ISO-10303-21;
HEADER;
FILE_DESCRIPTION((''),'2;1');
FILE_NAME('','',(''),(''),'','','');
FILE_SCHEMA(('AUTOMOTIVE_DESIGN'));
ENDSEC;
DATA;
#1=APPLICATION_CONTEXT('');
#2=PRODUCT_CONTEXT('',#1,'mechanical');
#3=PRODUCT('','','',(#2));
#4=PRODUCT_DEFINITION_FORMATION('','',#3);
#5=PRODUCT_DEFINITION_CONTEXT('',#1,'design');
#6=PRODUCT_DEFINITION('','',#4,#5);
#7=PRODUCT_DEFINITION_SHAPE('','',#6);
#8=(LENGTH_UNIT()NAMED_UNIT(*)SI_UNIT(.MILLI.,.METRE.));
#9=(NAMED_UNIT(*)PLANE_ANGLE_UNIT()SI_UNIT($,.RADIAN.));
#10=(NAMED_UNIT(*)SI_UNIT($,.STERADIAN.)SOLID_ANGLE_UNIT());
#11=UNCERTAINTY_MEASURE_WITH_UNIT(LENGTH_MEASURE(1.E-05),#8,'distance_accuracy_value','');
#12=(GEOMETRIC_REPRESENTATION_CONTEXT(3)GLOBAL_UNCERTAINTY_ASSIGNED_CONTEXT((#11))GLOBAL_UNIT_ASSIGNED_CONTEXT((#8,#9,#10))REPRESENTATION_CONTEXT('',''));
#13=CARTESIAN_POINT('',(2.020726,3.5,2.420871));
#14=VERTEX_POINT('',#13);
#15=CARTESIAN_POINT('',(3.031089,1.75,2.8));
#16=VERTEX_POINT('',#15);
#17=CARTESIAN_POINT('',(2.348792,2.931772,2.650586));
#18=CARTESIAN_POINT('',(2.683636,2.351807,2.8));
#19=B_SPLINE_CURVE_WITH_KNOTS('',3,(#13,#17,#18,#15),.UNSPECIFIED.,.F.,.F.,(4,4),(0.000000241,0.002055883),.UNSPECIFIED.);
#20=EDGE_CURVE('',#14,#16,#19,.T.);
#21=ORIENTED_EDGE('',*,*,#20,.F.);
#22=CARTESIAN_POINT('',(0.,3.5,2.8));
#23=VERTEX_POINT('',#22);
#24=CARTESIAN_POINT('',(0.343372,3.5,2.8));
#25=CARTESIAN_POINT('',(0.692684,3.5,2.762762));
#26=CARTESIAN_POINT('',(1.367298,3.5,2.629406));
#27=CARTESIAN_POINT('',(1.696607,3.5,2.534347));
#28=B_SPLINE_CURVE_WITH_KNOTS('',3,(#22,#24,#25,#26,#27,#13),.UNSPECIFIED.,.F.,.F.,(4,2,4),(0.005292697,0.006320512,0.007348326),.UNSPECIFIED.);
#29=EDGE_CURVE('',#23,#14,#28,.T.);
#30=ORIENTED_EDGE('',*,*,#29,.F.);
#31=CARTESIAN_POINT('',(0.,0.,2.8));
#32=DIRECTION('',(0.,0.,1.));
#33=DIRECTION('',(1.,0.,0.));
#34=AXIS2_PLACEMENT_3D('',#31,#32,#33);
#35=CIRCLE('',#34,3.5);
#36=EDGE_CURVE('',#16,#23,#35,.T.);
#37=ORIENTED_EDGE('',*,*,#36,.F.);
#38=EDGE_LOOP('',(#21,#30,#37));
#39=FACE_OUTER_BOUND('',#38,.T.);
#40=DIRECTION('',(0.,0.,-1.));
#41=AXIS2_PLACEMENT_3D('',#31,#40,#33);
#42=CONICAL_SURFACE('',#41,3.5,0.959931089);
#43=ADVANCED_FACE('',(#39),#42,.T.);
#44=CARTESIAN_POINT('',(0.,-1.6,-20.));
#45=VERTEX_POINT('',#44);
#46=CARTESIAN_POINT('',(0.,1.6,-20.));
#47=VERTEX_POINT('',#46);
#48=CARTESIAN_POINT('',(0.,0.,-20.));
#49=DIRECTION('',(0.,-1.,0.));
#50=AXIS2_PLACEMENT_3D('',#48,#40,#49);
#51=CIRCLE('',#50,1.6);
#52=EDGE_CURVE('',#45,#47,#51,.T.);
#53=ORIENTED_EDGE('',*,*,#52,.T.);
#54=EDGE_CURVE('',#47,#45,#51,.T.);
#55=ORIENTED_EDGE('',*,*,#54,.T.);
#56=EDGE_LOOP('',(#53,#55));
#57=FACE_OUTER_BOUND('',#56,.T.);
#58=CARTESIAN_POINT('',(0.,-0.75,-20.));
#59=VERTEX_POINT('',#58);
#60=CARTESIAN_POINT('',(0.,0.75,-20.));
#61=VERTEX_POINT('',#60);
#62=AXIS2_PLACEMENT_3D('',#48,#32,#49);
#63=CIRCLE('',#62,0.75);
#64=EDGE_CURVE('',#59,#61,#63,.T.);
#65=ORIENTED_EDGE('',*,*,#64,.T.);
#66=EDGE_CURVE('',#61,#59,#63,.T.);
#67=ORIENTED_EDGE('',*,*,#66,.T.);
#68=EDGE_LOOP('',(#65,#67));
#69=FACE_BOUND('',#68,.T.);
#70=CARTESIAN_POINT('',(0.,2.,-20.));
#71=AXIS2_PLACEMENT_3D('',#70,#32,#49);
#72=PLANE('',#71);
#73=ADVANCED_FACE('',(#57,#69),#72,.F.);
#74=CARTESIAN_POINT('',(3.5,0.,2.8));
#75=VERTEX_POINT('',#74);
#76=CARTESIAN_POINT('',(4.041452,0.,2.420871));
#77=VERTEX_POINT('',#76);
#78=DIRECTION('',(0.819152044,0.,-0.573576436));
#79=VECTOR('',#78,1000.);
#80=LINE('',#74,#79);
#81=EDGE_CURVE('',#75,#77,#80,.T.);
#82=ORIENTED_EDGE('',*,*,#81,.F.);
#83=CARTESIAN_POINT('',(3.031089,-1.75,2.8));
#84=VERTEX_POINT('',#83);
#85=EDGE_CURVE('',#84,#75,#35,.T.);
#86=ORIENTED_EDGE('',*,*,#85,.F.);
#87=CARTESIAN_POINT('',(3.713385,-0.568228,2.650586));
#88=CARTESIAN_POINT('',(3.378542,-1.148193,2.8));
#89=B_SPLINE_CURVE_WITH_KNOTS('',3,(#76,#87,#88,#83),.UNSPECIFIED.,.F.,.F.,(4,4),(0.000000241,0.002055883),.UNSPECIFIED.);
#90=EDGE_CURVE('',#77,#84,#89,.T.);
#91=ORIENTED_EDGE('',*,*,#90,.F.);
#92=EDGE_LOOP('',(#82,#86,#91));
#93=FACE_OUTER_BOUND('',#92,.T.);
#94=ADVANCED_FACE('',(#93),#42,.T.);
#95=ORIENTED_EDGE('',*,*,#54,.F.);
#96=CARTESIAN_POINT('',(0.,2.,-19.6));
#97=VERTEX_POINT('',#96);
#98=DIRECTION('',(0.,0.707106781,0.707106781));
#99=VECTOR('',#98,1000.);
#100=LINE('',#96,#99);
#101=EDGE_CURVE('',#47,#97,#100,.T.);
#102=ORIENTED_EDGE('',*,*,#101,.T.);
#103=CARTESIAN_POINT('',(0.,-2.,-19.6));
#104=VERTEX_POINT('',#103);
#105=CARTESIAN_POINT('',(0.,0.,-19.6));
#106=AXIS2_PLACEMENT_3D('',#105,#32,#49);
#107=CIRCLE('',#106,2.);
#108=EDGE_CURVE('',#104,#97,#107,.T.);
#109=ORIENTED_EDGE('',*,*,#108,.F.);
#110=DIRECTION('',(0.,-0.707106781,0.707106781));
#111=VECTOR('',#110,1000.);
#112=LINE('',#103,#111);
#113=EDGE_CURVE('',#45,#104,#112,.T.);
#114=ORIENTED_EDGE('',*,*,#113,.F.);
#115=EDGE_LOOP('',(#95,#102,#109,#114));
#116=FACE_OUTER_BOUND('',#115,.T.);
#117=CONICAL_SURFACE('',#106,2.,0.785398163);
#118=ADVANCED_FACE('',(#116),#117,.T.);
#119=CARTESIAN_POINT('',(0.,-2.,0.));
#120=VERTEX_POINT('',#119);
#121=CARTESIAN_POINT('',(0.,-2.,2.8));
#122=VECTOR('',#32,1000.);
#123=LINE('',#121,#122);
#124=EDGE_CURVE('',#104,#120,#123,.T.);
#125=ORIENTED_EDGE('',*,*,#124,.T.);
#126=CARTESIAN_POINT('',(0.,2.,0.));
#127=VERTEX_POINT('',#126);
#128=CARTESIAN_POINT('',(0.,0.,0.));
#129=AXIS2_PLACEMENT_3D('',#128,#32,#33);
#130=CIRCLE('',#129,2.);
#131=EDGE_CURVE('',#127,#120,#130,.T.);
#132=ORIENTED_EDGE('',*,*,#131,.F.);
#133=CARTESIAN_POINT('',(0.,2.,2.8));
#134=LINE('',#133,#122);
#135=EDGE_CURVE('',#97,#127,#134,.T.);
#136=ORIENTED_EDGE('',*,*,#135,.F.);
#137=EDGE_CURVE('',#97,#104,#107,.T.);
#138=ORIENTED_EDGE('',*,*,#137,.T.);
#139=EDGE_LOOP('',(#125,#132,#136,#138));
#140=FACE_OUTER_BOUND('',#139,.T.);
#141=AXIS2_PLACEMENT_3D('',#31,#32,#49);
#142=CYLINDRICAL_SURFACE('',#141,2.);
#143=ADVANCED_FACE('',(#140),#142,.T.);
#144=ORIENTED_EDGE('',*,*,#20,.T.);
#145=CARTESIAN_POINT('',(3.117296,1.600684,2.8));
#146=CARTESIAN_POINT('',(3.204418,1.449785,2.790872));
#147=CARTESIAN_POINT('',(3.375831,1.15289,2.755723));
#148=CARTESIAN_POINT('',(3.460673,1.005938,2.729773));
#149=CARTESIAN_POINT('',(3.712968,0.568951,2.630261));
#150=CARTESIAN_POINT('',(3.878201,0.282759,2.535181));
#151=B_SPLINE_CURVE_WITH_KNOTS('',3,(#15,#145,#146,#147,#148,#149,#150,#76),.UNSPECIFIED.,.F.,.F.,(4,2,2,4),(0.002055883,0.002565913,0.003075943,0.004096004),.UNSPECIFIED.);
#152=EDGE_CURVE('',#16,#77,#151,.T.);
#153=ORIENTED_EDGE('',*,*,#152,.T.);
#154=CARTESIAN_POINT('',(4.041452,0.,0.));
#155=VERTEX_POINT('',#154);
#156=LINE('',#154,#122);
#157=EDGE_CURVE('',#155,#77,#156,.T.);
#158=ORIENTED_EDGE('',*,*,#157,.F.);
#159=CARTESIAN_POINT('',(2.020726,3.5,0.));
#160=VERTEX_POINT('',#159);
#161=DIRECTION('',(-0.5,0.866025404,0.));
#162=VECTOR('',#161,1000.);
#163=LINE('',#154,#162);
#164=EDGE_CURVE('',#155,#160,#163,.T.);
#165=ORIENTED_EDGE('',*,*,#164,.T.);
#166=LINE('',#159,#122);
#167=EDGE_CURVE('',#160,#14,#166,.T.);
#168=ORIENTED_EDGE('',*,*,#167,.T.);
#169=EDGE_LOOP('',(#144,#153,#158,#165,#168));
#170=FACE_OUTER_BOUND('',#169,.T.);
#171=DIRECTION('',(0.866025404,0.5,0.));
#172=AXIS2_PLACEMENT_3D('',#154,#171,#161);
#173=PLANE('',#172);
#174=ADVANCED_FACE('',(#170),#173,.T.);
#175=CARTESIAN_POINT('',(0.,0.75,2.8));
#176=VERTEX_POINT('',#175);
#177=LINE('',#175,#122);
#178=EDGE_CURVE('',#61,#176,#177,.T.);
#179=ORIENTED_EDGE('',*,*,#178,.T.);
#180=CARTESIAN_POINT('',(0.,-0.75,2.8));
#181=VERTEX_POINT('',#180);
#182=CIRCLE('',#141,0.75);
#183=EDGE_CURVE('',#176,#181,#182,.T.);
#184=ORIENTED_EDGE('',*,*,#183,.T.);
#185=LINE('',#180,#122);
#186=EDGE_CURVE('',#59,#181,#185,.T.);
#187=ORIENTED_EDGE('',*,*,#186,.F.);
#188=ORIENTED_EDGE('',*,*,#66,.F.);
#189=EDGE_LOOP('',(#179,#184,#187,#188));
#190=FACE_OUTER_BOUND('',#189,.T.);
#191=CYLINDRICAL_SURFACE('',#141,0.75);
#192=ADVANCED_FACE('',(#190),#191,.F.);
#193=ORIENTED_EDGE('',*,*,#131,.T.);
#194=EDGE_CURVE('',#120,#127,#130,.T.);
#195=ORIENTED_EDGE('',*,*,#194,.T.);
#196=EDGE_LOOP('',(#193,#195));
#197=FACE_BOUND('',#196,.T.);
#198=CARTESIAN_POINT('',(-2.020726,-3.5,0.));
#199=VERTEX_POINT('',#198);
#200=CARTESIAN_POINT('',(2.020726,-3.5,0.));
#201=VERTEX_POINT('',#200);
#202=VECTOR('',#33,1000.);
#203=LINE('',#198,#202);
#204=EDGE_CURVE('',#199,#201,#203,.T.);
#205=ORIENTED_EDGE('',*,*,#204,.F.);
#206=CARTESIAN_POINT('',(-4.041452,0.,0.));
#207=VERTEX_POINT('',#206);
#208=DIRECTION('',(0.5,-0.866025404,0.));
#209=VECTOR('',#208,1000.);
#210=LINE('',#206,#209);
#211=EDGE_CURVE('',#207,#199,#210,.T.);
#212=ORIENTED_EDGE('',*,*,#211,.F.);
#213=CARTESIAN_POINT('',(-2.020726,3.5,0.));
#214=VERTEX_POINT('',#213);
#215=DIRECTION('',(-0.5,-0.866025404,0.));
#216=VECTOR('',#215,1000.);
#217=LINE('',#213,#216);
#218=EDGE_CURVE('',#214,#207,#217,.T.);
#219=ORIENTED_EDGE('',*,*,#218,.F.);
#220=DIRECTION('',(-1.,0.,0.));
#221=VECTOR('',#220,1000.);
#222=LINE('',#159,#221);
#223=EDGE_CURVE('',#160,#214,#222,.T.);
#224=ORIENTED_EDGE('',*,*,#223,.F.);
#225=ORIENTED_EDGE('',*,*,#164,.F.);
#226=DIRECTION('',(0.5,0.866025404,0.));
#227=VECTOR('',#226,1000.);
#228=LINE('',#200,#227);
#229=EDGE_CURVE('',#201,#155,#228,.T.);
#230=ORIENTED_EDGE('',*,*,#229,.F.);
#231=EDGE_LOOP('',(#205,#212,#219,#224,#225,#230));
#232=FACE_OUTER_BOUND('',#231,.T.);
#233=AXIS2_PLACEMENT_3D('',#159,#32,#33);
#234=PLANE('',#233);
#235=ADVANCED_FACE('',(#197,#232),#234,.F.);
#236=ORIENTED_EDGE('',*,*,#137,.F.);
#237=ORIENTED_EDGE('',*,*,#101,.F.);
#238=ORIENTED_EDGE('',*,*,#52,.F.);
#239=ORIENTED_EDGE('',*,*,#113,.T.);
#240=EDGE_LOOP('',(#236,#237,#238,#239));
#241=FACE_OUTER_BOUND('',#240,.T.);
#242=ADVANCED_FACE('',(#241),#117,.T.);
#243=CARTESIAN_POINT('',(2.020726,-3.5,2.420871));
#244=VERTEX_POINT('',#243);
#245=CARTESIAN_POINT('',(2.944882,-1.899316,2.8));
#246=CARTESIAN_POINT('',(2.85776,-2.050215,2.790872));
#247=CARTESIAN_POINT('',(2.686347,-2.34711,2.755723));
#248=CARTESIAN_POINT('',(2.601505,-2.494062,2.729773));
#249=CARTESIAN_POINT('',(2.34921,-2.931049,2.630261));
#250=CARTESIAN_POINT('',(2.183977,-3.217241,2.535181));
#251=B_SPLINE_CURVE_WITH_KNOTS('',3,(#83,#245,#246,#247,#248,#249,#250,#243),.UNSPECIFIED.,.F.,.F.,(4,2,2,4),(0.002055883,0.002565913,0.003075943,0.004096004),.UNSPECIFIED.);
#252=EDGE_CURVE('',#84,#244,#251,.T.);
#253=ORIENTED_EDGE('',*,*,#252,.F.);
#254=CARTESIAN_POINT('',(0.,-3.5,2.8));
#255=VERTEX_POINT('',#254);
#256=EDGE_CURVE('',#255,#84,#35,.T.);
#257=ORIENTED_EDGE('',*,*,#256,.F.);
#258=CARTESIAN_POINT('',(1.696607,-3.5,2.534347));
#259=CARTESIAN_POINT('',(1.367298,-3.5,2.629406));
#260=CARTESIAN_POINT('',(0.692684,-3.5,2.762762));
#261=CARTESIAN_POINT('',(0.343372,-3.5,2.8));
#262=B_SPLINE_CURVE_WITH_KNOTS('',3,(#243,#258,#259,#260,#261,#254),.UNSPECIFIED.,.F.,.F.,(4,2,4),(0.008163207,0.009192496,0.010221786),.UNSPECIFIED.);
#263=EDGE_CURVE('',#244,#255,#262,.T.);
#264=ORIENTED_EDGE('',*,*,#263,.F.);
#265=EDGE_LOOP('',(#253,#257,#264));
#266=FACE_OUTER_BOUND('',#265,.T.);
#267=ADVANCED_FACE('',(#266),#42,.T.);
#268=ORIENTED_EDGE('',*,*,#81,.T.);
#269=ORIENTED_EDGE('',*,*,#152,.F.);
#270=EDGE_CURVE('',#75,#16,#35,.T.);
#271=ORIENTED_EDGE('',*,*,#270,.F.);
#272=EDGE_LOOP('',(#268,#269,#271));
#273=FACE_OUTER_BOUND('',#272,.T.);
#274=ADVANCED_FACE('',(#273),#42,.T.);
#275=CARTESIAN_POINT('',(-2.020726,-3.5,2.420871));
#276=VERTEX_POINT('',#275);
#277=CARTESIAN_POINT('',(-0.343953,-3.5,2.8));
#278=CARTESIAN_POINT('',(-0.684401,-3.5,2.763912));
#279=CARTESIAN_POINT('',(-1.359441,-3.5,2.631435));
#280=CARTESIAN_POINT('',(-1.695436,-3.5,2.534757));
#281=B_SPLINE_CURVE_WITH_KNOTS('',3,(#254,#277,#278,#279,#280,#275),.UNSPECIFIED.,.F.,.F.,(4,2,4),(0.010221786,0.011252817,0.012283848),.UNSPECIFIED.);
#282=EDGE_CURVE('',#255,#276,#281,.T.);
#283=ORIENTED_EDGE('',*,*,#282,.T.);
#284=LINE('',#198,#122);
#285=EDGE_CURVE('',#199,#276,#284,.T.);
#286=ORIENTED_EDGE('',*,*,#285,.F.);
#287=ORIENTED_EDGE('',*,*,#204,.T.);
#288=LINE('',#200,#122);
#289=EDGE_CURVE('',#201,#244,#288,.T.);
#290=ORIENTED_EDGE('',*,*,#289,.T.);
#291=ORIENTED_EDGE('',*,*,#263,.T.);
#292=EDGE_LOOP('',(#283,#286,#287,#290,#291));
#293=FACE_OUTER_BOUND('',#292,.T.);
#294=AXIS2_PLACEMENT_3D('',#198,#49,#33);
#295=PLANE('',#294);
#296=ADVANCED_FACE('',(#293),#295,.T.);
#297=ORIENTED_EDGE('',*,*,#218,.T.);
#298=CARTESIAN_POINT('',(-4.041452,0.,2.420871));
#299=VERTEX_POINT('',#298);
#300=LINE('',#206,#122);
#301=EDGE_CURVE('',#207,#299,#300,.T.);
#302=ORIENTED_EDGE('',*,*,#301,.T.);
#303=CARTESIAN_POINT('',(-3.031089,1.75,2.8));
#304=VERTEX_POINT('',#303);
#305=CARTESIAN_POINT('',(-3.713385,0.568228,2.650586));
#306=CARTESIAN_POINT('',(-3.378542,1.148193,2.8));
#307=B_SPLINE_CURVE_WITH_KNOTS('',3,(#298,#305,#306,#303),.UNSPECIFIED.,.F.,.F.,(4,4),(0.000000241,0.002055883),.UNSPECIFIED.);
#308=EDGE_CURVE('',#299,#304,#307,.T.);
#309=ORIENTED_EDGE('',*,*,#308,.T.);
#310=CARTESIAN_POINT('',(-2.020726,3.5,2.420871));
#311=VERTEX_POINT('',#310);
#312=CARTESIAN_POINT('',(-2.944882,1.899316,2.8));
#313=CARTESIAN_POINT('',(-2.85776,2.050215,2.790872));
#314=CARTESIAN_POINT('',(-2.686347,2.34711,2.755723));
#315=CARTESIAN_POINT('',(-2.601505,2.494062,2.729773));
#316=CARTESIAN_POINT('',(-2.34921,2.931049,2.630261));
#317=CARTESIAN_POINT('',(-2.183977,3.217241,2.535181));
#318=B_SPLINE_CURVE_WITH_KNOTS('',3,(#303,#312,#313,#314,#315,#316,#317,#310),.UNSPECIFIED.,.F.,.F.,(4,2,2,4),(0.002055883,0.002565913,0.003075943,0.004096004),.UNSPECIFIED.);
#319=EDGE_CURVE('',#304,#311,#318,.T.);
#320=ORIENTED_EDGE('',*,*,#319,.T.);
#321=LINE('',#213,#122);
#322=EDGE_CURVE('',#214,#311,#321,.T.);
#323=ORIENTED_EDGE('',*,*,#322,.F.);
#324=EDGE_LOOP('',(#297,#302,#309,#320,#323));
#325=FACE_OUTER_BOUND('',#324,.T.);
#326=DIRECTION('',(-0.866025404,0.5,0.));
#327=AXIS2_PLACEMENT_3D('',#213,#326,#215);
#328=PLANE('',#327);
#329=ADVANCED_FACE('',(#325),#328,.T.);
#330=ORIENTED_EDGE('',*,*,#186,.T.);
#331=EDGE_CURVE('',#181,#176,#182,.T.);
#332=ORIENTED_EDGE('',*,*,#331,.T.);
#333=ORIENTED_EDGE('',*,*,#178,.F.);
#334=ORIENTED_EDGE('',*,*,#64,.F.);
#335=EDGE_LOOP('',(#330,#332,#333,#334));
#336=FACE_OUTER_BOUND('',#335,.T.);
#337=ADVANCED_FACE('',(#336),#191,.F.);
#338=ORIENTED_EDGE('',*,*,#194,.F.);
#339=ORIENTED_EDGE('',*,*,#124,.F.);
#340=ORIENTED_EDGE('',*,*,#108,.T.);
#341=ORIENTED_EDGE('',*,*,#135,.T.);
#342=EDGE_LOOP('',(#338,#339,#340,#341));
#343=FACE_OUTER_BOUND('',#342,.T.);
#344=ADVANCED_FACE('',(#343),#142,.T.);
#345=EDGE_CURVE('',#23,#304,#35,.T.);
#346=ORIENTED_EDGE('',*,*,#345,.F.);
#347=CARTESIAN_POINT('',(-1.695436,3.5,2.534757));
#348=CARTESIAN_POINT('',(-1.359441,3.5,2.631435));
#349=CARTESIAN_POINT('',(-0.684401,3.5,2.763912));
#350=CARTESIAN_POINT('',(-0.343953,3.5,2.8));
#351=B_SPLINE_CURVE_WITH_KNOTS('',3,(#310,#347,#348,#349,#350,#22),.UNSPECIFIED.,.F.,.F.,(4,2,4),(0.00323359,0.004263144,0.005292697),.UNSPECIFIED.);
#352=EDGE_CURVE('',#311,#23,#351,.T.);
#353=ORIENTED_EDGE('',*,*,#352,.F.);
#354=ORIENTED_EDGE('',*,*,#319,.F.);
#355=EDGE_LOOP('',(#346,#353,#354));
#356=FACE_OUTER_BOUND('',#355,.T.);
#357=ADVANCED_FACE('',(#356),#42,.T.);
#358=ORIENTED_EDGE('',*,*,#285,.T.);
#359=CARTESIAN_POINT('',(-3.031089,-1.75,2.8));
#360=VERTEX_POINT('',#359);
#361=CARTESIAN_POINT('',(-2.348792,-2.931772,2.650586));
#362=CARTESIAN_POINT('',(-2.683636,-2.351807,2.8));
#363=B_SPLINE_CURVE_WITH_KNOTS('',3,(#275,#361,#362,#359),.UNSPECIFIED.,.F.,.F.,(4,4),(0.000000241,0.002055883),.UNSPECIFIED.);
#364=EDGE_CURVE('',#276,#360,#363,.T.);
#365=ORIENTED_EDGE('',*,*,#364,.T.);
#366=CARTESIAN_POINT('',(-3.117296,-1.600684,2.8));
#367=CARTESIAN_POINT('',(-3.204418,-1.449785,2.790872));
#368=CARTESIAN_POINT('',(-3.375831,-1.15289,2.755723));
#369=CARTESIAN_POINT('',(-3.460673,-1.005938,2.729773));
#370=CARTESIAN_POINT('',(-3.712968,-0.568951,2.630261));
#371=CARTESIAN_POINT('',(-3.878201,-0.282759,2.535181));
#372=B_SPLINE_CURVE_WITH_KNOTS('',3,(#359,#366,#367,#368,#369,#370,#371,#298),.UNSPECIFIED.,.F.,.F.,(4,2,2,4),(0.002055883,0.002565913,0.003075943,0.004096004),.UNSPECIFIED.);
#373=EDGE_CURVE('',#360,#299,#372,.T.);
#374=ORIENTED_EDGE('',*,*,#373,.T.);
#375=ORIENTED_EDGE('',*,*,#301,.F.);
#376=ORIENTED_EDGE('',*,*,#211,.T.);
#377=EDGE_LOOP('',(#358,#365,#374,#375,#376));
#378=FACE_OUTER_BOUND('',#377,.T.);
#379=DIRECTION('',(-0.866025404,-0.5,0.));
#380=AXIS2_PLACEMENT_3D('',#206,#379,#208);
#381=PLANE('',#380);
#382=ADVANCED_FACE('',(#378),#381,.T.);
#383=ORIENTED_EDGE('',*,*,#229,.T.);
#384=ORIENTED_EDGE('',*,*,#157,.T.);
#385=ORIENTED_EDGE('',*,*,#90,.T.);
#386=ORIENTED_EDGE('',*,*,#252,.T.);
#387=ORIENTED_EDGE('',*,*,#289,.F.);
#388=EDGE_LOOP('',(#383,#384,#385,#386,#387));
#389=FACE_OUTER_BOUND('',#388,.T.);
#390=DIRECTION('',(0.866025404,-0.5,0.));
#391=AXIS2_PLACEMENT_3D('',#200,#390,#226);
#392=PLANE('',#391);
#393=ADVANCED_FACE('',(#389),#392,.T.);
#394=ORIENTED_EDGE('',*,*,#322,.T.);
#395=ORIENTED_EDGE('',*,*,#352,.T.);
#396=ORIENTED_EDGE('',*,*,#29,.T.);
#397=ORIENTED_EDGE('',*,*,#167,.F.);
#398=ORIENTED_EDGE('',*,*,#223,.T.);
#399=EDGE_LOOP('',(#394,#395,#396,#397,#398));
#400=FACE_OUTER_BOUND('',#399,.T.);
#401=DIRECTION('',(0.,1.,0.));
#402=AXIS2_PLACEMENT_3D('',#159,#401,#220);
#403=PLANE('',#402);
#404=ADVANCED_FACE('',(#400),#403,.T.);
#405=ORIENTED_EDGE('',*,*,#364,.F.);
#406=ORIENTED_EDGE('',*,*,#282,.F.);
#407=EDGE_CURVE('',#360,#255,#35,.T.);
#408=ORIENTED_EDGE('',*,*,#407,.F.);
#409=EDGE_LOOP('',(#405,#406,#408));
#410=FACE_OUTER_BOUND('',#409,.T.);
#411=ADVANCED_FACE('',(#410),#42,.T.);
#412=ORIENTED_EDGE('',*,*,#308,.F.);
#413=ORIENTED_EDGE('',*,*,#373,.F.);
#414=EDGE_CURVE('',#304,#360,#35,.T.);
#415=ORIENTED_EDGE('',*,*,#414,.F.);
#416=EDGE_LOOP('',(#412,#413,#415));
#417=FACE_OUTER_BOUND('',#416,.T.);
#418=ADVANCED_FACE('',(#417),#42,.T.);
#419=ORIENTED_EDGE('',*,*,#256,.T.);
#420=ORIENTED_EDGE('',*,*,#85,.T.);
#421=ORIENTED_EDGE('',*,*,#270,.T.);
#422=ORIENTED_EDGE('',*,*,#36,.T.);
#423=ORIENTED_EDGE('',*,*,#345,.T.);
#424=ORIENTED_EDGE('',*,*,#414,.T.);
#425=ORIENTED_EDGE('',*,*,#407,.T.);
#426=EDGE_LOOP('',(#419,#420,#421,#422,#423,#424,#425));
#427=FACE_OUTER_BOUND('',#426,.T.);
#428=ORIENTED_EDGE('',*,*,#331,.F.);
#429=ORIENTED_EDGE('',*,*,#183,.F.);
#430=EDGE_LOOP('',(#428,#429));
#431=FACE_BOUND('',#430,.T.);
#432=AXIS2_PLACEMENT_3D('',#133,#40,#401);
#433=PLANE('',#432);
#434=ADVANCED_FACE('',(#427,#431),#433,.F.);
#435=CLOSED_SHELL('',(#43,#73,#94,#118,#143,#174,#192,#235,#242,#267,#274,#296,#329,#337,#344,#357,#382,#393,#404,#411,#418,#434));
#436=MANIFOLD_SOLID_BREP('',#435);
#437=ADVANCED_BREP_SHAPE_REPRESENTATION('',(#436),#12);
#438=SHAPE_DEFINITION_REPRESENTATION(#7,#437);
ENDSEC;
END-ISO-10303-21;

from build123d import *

# Parameters (mm, degrees)
BOSS_EXTRUDE1_START = -2.8
SKETCH4_R           = 0.75
BOSS_EXTRUDE1_DEPTH = 2.8
SKETCH5_R           = 4.582903769
SKETCH5_R_2         = 3.5
CUT_EXTRUDE1_DEPTH  = 1
CUT_EXTRUDE1_DRAFT  = -55
CHAMFER1_SIZE       = 0.4


with BuildPart() as part:
    # Sketch3 → Revolve1 (revolve)
    with BuildSketch(Plane(origin=(0, 0, 0), x_dir=(0, 0, -1), z_dir=(1, 0, 0)), mode=Mode.PRIVATE) as revolve1_sk:
        Polygon((0, 2), (-2.8, 2), (-2.8, 0.75), (20, 0.75), (20, 2), align=None)
    revolve(revolve1_sk.sketch.rotate(Axis((0, 0, 2.8), (0, 0, -1)), 180), axis=Axis((0, 0, 2.8), (0, 0, -1)))

    # Sketch4 → Boss-Extrude1 (add)
    with BuildSketch(Plane.XY.offset(2.8).offset(BOSS_EXTRUDE1_START)):
        Polygon((2.020725942, 3.5), (-2.020725942, 3.5), (-4.041451884, 0), (-2.020725942, -3.5), (2.020725942, -3.5), (4.041451884, 0), align=None)
        with Locations(Location((0, 0, 0), (0, 0, 270))):
            Circle(SKETCH4_R, mode=Mode.SUBTRACT)
    extrude(amount=BOSS_EXTRUDE1_DEPTH)


with BuildPart() as cut_extrude1_tool:
    # Sketch5 → Cut-Extrude1 (with draft: the straight prism first)
    with BuildSketch(Plane.XY.offset(2.8)):
        Circle(SKETCH5_R)
        Circle(SKETCH5_R_2, mode=Mode.SUBTRACT)
    extrude(amount=-CUT_EXTRUDE1_DEPTH)
    # Cut-Extrude1: the draft: its side faces are tilted about the plane it starts from
    cut_extrude1_sides = [cut_extrude1_tool.faces().sort_by_distance(p)[0] for p in [
        (-4.582903769, 0, 2.3),
        (-3.5, 0, 2.3),
    ]]
    draft(cut_extrude1_sides, Plane.XY.offset(2.8), CUT_EXTRUDE1_DRAFT)


with BuildPart() as part_1:
    add(part.part)

    # Cut-Extrude1: cut by cut_extrude1_tool
    add(cut_extrude1_tool.part, mode=Mode.SUBTRACT)

    # Chamfer1
    chamfer1_edges = [part_1.edges().sort_by_distance(p)[0] for p in [
        (0, 2, -20),
    ]]
    chamfer(chamfer1_edges, length=CHAMFER1_SIZE)


solid = part_1.part
